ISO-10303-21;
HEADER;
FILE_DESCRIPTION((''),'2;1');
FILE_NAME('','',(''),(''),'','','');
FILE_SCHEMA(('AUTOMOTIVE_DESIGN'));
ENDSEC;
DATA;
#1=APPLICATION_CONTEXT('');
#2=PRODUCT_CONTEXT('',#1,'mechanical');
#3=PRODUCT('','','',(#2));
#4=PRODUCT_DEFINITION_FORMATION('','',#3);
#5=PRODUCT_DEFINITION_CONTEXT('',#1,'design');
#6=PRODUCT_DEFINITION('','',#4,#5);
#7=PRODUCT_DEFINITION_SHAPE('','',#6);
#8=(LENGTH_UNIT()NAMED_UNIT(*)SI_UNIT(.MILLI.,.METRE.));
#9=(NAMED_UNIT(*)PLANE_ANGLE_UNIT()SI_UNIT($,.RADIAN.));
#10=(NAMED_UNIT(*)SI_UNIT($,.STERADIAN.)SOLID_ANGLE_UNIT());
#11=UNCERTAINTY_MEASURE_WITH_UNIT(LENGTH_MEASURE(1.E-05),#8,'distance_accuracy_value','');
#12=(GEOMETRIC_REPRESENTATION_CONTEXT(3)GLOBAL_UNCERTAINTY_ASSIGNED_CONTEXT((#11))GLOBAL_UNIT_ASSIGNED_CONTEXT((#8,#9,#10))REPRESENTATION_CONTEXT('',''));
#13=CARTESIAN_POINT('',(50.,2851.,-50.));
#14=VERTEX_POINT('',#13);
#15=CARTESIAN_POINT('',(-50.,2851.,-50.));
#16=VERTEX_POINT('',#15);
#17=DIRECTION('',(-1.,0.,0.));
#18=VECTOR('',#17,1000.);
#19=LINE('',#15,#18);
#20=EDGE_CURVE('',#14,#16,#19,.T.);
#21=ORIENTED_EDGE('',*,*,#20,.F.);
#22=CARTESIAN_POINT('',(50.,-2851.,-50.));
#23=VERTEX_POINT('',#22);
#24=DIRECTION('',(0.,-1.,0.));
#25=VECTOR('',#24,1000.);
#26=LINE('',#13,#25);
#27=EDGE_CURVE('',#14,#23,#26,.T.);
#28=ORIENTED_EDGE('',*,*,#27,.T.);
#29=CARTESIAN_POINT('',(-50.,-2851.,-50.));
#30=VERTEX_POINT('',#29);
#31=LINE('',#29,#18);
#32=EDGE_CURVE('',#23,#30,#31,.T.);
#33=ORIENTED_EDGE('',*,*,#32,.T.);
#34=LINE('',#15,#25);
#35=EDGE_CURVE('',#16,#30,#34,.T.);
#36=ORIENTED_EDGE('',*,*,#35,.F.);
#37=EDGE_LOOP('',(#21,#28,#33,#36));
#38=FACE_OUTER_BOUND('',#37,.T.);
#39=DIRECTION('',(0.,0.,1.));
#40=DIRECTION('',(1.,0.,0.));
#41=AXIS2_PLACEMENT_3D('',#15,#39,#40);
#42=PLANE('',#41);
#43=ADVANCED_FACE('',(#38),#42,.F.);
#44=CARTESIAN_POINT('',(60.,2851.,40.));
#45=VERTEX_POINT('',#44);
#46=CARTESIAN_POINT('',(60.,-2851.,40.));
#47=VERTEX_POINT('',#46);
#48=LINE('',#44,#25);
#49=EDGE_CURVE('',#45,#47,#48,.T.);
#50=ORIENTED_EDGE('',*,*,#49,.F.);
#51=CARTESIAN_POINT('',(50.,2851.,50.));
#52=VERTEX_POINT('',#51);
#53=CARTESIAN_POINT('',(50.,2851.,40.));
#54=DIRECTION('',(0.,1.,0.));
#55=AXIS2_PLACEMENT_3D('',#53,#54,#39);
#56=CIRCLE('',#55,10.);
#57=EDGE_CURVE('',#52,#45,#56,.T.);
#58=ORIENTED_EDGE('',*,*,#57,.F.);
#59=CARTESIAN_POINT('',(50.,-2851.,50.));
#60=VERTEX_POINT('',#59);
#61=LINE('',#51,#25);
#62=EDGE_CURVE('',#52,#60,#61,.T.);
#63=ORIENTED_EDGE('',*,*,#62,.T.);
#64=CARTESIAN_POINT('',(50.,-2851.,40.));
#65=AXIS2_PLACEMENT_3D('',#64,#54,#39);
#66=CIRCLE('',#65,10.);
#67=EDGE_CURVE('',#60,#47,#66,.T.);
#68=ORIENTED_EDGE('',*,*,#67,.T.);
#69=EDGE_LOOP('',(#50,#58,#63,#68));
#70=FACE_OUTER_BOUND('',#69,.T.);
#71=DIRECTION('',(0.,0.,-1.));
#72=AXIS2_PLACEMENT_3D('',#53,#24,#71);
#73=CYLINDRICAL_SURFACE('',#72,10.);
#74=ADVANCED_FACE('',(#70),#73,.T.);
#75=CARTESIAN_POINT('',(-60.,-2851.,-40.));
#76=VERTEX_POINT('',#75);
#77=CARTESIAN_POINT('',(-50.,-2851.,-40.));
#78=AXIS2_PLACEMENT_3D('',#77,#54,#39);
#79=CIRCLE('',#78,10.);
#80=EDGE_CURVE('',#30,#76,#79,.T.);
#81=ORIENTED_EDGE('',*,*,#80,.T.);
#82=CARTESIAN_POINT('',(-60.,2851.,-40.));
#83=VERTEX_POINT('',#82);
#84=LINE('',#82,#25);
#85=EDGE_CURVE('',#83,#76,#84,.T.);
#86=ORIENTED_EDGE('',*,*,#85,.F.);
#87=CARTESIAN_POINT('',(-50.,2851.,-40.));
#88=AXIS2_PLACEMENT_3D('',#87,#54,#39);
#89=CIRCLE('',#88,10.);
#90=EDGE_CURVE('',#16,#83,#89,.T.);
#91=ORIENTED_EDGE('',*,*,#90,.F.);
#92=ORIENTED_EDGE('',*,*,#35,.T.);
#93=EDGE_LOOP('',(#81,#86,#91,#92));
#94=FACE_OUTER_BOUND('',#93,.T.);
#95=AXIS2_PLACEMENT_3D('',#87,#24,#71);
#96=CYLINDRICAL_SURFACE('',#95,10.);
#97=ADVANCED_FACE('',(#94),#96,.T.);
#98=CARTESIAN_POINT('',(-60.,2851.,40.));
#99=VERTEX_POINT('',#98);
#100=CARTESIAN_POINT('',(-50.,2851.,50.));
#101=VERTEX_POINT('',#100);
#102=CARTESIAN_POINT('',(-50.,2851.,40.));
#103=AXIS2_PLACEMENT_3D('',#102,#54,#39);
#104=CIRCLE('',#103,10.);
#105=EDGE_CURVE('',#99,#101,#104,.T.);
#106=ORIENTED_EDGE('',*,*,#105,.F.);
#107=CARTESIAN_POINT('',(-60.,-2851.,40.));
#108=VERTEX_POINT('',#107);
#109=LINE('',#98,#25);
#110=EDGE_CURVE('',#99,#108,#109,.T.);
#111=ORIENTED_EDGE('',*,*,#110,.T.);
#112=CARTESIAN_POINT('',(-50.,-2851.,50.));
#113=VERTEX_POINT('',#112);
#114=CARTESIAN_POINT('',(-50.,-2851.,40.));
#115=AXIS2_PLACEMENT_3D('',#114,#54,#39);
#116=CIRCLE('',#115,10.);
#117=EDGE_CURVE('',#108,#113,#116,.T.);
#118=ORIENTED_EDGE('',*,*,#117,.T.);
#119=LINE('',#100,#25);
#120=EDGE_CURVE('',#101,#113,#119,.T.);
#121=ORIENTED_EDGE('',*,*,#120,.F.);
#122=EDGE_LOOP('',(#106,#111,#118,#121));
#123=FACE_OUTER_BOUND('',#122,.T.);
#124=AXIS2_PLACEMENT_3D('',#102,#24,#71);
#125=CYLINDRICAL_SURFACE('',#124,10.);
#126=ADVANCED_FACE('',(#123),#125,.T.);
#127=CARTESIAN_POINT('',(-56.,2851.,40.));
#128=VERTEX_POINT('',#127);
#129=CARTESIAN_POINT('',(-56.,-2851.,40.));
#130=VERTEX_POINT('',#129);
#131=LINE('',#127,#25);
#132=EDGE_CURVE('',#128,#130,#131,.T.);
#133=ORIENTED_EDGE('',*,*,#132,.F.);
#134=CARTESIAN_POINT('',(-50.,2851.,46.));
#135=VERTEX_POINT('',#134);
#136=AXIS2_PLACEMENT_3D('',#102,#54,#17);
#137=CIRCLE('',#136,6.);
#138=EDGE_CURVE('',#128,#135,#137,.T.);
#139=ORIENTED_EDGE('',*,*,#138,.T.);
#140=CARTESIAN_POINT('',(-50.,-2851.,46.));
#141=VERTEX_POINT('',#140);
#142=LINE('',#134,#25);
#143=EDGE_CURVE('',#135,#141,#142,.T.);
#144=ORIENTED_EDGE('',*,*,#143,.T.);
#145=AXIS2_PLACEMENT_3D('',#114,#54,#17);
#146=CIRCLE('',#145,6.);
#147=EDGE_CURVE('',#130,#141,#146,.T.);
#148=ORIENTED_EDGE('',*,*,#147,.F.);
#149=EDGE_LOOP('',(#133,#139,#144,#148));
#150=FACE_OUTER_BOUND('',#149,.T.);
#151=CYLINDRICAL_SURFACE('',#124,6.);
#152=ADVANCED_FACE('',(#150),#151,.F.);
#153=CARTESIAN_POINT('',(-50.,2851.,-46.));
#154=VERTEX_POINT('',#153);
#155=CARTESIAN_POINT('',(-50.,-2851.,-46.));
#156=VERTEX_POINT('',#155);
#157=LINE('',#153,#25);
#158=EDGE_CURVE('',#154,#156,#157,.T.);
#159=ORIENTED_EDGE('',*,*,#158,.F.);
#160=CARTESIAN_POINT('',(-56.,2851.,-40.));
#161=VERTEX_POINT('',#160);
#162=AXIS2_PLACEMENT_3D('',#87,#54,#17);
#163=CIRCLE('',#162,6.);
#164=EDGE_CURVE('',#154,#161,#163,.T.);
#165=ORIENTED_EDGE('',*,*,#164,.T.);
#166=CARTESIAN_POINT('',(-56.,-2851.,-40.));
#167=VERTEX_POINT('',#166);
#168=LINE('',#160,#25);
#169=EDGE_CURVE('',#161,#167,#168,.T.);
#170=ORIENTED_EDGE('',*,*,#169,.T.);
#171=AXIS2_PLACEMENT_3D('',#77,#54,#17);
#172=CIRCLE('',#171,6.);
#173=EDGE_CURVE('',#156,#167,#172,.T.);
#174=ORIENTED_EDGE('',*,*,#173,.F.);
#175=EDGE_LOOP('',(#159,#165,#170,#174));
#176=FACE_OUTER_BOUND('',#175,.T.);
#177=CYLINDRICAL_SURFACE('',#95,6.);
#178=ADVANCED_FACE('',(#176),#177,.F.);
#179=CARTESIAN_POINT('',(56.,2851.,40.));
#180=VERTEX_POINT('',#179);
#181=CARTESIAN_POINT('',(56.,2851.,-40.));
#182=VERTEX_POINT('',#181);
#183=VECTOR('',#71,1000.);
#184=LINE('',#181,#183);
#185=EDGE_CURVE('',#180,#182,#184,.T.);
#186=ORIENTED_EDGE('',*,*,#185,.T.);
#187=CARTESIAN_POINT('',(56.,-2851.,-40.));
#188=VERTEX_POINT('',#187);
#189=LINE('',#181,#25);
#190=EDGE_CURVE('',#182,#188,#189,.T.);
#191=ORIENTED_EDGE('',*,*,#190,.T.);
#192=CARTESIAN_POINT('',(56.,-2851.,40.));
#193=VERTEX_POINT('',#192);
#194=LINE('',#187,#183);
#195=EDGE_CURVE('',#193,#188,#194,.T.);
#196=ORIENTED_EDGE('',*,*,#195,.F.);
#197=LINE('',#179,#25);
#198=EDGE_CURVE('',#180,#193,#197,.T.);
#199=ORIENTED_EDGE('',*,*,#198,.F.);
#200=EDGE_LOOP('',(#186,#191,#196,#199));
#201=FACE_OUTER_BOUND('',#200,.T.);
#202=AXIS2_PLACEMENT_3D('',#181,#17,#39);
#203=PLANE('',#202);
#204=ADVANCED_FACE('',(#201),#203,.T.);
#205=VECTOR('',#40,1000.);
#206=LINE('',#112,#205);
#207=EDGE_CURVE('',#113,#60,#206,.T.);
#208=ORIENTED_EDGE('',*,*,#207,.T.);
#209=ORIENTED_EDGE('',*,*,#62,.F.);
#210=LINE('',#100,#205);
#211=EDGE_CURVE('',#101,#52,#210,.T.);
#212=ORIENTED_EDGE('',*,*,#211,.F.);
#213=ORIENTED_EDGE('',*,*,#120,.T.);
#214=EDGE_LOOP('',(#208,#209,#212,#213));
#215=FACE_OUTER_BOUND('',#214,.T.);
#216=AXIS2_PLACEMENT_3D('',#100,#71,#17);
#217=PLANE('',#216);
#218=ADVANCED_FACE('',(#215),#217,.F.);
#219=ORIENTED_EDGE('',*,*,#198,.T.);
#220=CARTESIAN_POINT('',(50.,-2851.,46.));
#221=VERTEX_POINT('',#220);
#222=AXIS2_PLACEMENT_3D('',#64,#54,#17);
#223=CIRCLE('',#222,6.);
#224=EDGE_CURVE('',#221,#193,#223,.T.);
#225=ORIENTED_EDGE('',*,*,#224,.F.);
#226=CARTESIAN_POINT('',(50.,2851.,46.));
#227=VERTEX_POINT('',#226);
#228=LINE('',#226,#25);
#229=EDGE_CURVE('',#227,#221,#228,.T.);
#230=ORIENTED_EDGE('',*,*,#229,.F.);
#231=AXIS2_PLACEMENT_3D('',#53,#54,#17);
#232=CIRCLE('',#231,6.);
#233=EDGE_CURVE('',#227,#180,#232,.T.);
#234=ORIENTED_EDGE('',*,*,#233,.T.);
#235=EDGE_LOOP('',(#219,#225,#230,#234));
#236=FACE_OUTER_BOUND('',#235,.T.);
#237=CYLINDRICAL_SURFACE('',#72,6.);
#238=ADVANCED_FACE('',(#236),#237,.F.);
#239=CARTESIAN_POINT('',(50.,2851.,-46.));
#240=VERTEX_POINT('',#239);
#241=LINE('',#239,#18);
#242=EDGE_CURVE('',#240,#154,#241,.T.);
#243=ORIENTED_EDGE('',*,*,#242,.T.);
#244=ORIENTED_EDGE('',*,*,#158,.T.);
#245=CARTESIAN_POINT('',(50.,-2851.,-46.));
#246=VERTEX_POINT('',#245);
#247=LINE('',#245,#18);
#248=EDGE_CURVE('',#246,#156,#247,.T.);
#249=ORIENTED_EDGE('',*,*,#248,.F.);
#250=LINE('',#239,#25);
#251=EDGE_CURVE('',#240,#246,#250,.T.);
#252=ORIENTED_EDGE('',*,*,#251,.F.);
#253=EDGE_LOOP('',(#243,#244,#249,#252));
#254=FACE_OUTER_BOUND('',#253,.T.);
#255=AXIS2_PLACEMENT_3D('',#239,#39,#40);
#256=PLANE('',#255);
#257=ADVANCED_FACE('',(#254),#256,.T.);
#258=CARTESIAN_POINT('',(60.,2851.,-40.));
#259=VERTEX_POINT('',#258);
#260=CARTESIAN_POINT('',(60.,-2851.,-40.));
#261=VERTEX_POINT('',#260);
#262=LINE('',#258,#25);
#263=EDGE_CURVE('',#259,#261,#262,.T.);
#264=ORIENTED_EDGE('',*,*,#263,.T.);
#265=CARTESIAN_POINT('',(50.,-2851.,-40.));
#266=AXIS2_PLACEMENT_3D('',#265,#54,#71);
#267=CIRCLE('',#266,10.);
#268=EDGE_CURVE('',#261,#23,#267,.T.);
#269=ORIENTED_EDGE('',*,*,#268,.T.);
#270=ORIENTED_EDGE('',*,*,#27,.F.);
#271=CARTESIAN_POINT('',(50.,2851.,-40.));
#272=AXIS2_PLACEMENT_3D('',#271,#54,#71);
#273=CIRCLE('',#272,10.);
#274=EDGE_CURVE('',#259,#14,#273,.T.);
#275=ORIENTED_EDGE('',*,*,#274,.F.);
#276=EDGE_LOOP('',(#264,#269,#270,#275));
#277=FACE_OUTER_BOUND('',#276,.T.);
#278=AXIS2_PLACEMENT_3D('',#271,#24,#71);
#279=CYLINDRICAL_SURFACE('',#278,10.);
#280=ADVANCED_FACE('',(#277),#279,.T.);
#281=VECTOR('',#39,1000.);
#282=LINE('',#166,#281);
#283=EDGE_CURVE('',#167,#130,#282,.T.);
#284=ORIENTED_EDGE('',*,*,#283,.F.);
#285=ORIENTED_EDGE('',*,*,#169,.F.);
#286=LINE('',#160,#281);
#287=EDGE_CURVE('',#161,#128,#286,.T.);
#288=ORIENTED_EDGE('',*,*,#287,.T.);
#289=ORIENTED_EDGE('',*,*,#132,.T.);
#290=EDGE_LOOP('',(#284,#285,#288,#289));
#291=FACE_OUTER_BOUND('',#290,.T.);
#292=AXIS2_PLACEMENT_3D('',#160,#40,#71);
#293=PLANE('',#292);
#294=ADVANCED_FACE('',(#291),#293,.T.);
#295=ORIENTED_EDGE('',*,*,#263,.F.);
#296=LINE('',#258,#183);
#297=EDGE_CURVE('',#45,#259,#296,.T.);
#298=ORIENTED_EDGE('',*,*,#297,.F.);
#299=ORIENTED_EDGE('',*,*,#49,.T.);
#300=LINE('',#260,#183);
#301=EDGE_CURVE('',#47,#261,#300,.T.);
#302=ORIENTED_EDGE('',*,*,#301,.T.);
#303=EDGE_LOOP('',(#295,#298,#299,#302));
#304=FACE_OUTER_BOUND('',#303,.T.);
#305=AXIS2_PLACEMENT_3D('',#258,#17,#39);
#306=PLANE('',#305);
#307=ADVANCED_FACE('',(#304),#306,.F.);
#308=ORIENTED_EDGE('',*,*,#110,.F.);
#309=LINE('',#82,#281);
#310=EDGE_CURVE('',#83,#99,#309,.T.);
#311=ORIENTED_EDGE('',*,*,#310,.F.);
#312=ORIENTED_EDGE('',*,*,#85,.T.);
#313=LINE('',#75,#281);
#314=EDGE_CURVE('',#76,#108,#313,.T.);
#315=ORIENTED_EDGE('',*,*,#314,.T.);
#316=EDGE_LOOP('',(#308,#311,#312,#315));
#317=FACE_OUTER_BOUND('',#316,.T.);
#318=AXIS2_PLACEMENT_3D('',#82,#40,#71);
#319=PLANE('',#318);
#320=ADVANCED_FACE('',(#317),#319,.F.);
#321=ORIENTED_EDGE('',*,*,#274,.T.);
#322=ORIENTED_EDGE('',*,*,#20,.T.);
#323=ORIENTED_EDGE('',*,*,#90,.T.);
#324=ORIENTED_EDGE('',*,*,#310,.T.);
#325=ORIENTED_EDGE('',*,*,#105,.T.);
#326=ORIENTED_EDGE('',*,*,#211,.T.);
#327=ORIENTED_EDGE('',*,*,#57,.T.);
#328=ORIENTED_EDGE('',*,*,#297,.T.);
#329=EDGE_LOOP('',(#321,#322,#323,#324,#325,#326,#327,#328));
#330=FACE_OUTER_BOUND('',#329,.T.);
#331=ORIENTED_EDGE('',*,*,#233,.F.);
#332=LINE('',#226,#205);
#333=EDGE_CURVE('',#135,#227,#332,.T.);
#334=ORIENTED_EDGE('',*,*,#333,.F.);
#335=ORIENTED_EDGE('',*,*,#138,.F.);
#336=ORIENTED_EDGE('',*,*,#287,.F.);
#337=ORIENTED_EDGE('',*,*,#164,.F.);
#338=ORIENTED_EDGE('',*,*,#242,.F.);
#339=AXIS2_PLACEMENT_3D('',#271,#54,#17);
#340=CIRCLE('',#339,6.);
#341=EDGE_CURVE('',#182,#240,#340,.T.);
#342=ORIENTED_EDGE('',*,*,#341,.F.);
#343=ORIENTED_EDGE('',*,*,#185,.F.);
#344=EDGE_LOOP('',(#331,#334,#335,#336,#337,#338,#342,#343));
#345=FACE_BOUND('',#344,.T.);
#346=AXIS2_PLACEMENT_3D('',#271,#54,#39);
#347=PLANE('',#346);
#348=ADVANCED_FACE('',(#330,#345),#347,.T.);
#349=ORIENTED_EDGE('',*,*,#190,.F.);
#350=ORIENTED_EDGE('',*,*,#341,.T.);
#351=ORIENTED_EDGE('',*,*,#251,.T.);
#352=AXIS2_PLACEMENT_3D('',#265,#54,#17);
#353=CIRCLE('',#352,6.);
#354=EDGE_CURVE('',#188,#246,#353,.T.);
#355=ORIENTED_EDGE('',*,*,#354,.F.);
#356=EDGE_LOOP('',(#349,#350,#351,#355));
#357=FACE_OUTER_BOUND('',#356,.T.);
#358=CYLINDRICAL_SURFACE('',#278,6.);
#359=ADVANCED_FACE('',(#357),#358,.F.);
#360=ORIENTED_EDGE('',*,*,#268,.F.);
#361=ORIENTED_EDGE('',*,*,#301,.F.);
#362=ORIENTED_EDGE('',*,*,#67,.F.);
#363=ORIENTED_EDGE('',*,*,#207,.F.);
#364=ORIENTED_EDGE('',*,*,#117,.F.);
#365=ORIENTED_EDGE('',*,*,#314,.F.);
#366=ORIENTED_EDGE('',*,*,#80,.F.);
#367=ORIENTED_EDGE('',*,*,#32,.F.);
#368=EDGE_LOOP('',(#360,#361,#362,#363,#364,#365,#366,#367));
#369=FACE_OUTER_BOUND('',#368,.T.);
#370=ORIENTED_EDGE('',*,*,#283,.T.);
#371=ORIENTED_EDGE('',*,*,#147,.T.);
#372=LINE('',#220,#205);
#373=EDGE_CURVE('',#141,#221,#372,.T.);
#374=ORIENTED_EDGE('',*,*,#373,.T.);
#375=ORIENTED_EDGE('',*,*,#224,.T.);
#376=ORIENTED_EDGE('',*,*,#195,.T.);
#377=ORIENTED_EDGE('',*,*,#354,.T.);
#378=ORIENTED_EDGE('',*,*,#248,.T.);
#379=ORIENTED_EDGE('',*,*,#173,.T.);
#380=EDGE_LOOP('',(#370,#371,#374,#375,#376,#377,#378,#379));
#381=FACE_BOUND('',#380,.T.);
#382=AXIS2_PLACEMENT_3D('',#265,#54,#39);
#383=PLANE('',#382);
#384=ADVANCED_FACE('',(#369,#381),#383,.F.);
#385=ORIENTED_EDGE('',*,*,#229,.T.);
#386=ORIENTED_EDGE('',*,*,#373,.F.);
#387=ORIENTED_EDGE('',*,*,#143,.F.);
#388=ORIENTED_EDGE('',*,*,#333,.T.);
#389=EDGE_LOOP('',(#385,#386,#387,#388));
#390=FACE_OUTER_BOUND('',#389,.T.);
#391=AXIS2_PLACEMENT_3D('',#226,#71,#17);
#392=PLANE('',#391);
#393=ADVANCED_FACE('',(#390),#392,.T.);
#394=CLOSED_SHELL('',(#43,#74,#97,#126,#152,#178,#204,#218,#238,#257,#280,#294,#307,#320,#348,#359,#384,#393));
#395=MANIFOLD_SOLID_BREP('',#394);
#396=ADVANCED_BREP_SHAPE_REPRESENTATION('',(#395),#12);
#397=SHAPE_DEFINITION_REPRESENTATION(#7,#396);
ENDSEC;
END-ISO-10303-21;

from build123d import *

# Parameters (mm, degrees)
EXTRUDE_THIN1_DEPTH = 2851


with BuildPart() as part:
    # Sketch1 → Extrude-Thin1 (new, symmetric)
    with BuildSketch(Plane(origin=(0, 0, 0), x_dir=(1, 0, 0), z_dir=(0, 1, 0))):
        with BuildLine():
            Line((-50, 50), (50, 50))
            ThreePointArc((50, 50), (57.071067812, 47.071067812), (60, 40))
            Line((60, 40), (60, -40))
            ThreePointArc((60, -40), (57.071067812, -47.071067812), (50, -50))
            Line((50, -50), (-50, -50))
            ThreePointArc((-50, -50), (-57.071067812, -47.071067812), (-60, -40))
            Line((-60, -40), (-60, 40))
            ThreePointArc((-60, 40), (-57.071067812, 47.071067812), (-50, 50))
        make_face()
        with BuildLine():
            Line((-50, 46), (50, 46))
            ThreePointArc((50, 46), (54.242640687, 44.242640687), (56, 40))
            Line((56, 40), (56, -40))
            ThreePointArc((56, -40), (54.242640687, -44.242640687), (50, -46))
            Line((50, -46), (-50, -46))
            ThreePointArc((-50, -46), (-54.242640687, -44.242640687), (-56, -40))
            Line((-56, -40), (-56, 40))
            ThreePointArc((-56, 40), (-54.242640687, 44.242640687), (-50, 46))
        make_face(mode=Mode.SUBTRACT)
    extrude(amount=EXTRUDE_THIN1_DEPTH, both=True)


solid = part.part
